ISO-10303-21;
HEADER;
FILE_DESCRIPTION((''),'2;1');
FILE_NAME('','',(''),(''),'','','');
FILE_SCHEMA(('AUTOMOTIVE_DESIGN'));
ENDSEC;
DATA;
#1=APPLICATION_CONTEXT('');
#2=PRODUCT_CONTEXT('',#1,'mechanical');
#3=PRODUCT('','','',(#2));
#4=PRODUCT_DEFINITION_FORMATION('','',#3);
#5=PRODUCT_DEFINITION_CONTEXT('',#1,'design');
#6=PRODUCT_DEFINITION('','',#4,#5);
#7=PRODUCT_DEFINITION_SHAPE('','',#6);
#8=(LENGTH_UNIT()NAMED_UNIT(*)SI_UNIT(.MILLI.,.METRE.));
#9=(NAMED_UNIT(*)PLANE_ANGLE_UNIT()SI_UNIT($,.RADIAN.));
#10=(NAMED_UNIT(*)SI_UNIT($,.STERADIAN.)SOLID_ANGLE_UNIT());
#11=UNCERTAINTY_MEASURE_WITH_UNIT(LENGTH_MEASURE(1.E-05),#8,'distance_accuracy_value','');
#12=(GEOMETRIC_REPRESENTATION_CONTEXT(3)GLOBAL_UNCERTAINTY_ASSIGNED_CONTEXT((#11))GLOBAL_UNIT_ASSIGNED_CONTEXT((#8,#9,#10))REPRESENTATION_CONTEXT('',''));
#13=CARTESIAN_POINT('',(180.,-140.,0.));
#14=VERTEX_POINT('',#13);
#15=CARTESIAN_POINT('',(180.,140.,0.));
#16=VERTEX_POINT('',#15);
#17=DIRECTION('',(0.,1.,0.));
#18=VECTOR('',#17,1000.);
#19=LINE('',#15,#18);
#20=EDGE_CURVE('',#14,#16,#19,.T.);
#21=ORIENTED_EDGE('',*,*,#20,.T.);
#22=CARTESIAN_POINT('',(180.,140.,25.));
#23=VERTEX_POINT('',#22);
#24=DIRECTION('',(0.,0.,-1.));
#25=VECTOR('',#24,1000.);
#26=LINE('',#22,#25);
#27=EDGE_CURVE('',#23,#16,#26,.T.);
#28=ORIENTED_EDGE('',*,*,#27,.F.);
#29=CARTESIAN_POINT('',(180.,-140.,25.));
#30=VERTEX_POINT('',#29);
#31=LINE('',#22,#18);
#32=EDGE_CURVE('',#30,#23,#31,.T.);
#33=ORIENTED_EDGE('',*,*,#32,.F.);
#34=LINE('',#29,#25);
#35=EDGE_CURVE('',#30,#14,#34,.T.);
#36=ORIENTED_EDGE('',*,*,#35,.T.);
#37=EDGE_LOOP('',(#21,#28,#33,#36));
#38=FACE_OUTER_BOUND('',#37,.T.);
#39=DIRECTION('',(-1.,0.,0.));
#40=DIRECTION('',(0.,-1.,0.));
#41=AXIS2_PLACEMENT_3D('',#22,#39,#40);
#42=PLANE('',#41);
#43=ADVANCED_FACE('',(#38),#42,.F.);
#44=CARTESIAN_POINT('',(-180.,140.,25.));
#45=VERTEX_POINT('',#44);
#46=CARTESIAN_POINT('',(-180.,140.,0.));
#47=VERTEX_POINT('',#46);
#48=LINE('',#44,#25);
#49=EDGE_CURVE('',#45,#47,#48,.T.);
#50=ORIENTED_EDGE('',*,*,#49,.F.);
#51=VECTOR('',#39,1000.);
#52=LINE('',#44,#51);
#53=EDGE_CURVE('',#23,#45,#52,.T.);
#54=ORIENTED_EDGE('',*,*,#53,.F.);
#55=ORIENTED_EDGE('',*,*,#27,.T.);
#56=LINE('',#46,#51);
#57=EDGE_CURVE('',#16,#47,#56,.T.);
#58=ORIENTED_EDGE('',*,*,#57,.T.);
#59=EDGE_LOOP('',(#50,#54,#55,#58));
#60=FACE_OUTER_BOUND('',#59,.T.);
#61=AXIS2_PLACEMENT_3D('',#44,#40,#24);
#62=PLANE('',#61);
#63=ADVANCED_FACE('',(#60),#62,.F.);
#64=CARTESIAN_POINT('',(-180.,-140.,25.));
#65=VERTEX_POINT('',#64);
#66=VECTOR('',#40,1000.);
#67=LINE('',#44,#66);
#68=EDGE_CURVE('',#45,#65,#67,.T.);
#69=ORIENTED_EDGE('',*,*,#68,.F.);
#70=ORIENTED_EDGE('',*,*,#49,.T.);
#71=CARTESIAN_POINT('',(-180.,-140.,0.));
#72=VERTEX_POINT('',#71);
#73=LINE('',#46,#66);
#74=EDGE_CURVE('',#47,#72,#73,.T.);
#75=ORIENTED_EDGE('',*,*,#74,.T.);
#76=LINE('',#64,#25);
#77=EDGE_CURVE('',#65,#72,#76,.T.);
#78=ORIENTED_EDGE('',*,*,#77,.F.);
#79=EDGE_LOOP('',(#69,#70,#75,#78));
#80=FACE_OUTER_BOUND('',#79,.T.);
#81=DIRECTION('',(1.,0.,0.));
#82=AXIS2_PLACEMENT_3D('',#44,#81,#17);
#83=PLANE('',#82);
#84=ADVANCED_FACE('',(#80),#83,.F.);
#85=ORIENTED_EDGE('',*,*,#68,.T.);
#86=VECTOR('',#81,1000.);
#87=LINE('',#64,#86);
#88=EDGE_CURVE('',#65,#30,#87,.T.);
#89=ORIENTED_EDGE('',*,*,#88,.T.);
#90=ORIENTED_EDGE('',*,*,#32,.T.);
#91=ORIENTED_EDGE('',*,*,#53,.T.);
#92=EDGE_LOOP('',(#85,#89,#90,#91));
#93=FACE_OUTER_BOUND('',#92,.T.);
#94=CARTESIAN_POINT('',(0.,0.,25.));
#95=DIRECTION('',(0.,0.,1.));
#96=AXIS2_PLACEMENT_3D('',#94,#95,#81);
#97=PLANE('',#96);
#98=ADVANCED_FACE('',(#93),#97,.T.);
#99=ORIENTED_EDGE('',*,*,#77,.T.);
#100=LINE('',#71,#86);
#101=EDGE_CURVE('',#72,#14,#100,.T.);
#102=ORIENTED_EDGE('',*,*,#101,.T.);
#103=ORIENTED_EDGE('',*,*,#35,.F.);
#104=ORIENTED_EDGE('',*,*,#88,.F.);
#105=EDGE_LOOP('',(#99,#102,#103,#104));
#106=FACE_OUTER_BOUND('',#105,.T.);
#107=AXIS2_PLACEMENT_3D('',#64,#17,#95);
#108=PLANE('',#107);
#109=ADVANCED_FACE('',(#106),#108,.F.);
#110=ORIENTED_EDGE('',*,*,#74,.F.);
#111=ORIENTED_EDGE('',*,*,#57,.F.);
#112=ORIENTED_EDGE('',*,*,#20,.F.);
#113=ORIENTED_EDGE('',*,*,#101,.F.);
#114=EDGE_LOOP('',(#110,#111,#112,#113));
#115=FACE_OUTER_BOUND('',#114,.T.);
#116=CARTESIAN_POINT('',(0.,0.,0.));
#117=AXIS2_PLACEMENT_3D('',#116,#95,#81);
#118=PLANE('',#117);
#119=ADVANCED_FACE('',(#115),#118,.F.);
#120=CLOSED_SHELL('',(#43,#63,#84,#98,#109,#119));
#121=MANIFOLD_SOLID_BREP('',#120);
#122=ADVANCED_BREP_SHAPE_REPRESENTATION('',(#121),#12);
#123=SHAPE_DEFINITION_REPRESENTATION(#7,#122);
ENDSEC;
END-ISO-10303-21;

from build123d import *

# Parameters (mm, degrees)
SKETCH_1_W      = 360
SKETCH_1_H      = 280
EXTRUDE_1_DEPTH = 25


with BuildPart() as part:
    # 草图1 → 凸台-拉伸1 (new body)
    with BuildSketch(Plane.XY):
        Rectangle(SKETCH_1_W, SKETCH_1_H)
    extrude(amount=EXTRUDE_1_DEPTH)


solid = part.part
